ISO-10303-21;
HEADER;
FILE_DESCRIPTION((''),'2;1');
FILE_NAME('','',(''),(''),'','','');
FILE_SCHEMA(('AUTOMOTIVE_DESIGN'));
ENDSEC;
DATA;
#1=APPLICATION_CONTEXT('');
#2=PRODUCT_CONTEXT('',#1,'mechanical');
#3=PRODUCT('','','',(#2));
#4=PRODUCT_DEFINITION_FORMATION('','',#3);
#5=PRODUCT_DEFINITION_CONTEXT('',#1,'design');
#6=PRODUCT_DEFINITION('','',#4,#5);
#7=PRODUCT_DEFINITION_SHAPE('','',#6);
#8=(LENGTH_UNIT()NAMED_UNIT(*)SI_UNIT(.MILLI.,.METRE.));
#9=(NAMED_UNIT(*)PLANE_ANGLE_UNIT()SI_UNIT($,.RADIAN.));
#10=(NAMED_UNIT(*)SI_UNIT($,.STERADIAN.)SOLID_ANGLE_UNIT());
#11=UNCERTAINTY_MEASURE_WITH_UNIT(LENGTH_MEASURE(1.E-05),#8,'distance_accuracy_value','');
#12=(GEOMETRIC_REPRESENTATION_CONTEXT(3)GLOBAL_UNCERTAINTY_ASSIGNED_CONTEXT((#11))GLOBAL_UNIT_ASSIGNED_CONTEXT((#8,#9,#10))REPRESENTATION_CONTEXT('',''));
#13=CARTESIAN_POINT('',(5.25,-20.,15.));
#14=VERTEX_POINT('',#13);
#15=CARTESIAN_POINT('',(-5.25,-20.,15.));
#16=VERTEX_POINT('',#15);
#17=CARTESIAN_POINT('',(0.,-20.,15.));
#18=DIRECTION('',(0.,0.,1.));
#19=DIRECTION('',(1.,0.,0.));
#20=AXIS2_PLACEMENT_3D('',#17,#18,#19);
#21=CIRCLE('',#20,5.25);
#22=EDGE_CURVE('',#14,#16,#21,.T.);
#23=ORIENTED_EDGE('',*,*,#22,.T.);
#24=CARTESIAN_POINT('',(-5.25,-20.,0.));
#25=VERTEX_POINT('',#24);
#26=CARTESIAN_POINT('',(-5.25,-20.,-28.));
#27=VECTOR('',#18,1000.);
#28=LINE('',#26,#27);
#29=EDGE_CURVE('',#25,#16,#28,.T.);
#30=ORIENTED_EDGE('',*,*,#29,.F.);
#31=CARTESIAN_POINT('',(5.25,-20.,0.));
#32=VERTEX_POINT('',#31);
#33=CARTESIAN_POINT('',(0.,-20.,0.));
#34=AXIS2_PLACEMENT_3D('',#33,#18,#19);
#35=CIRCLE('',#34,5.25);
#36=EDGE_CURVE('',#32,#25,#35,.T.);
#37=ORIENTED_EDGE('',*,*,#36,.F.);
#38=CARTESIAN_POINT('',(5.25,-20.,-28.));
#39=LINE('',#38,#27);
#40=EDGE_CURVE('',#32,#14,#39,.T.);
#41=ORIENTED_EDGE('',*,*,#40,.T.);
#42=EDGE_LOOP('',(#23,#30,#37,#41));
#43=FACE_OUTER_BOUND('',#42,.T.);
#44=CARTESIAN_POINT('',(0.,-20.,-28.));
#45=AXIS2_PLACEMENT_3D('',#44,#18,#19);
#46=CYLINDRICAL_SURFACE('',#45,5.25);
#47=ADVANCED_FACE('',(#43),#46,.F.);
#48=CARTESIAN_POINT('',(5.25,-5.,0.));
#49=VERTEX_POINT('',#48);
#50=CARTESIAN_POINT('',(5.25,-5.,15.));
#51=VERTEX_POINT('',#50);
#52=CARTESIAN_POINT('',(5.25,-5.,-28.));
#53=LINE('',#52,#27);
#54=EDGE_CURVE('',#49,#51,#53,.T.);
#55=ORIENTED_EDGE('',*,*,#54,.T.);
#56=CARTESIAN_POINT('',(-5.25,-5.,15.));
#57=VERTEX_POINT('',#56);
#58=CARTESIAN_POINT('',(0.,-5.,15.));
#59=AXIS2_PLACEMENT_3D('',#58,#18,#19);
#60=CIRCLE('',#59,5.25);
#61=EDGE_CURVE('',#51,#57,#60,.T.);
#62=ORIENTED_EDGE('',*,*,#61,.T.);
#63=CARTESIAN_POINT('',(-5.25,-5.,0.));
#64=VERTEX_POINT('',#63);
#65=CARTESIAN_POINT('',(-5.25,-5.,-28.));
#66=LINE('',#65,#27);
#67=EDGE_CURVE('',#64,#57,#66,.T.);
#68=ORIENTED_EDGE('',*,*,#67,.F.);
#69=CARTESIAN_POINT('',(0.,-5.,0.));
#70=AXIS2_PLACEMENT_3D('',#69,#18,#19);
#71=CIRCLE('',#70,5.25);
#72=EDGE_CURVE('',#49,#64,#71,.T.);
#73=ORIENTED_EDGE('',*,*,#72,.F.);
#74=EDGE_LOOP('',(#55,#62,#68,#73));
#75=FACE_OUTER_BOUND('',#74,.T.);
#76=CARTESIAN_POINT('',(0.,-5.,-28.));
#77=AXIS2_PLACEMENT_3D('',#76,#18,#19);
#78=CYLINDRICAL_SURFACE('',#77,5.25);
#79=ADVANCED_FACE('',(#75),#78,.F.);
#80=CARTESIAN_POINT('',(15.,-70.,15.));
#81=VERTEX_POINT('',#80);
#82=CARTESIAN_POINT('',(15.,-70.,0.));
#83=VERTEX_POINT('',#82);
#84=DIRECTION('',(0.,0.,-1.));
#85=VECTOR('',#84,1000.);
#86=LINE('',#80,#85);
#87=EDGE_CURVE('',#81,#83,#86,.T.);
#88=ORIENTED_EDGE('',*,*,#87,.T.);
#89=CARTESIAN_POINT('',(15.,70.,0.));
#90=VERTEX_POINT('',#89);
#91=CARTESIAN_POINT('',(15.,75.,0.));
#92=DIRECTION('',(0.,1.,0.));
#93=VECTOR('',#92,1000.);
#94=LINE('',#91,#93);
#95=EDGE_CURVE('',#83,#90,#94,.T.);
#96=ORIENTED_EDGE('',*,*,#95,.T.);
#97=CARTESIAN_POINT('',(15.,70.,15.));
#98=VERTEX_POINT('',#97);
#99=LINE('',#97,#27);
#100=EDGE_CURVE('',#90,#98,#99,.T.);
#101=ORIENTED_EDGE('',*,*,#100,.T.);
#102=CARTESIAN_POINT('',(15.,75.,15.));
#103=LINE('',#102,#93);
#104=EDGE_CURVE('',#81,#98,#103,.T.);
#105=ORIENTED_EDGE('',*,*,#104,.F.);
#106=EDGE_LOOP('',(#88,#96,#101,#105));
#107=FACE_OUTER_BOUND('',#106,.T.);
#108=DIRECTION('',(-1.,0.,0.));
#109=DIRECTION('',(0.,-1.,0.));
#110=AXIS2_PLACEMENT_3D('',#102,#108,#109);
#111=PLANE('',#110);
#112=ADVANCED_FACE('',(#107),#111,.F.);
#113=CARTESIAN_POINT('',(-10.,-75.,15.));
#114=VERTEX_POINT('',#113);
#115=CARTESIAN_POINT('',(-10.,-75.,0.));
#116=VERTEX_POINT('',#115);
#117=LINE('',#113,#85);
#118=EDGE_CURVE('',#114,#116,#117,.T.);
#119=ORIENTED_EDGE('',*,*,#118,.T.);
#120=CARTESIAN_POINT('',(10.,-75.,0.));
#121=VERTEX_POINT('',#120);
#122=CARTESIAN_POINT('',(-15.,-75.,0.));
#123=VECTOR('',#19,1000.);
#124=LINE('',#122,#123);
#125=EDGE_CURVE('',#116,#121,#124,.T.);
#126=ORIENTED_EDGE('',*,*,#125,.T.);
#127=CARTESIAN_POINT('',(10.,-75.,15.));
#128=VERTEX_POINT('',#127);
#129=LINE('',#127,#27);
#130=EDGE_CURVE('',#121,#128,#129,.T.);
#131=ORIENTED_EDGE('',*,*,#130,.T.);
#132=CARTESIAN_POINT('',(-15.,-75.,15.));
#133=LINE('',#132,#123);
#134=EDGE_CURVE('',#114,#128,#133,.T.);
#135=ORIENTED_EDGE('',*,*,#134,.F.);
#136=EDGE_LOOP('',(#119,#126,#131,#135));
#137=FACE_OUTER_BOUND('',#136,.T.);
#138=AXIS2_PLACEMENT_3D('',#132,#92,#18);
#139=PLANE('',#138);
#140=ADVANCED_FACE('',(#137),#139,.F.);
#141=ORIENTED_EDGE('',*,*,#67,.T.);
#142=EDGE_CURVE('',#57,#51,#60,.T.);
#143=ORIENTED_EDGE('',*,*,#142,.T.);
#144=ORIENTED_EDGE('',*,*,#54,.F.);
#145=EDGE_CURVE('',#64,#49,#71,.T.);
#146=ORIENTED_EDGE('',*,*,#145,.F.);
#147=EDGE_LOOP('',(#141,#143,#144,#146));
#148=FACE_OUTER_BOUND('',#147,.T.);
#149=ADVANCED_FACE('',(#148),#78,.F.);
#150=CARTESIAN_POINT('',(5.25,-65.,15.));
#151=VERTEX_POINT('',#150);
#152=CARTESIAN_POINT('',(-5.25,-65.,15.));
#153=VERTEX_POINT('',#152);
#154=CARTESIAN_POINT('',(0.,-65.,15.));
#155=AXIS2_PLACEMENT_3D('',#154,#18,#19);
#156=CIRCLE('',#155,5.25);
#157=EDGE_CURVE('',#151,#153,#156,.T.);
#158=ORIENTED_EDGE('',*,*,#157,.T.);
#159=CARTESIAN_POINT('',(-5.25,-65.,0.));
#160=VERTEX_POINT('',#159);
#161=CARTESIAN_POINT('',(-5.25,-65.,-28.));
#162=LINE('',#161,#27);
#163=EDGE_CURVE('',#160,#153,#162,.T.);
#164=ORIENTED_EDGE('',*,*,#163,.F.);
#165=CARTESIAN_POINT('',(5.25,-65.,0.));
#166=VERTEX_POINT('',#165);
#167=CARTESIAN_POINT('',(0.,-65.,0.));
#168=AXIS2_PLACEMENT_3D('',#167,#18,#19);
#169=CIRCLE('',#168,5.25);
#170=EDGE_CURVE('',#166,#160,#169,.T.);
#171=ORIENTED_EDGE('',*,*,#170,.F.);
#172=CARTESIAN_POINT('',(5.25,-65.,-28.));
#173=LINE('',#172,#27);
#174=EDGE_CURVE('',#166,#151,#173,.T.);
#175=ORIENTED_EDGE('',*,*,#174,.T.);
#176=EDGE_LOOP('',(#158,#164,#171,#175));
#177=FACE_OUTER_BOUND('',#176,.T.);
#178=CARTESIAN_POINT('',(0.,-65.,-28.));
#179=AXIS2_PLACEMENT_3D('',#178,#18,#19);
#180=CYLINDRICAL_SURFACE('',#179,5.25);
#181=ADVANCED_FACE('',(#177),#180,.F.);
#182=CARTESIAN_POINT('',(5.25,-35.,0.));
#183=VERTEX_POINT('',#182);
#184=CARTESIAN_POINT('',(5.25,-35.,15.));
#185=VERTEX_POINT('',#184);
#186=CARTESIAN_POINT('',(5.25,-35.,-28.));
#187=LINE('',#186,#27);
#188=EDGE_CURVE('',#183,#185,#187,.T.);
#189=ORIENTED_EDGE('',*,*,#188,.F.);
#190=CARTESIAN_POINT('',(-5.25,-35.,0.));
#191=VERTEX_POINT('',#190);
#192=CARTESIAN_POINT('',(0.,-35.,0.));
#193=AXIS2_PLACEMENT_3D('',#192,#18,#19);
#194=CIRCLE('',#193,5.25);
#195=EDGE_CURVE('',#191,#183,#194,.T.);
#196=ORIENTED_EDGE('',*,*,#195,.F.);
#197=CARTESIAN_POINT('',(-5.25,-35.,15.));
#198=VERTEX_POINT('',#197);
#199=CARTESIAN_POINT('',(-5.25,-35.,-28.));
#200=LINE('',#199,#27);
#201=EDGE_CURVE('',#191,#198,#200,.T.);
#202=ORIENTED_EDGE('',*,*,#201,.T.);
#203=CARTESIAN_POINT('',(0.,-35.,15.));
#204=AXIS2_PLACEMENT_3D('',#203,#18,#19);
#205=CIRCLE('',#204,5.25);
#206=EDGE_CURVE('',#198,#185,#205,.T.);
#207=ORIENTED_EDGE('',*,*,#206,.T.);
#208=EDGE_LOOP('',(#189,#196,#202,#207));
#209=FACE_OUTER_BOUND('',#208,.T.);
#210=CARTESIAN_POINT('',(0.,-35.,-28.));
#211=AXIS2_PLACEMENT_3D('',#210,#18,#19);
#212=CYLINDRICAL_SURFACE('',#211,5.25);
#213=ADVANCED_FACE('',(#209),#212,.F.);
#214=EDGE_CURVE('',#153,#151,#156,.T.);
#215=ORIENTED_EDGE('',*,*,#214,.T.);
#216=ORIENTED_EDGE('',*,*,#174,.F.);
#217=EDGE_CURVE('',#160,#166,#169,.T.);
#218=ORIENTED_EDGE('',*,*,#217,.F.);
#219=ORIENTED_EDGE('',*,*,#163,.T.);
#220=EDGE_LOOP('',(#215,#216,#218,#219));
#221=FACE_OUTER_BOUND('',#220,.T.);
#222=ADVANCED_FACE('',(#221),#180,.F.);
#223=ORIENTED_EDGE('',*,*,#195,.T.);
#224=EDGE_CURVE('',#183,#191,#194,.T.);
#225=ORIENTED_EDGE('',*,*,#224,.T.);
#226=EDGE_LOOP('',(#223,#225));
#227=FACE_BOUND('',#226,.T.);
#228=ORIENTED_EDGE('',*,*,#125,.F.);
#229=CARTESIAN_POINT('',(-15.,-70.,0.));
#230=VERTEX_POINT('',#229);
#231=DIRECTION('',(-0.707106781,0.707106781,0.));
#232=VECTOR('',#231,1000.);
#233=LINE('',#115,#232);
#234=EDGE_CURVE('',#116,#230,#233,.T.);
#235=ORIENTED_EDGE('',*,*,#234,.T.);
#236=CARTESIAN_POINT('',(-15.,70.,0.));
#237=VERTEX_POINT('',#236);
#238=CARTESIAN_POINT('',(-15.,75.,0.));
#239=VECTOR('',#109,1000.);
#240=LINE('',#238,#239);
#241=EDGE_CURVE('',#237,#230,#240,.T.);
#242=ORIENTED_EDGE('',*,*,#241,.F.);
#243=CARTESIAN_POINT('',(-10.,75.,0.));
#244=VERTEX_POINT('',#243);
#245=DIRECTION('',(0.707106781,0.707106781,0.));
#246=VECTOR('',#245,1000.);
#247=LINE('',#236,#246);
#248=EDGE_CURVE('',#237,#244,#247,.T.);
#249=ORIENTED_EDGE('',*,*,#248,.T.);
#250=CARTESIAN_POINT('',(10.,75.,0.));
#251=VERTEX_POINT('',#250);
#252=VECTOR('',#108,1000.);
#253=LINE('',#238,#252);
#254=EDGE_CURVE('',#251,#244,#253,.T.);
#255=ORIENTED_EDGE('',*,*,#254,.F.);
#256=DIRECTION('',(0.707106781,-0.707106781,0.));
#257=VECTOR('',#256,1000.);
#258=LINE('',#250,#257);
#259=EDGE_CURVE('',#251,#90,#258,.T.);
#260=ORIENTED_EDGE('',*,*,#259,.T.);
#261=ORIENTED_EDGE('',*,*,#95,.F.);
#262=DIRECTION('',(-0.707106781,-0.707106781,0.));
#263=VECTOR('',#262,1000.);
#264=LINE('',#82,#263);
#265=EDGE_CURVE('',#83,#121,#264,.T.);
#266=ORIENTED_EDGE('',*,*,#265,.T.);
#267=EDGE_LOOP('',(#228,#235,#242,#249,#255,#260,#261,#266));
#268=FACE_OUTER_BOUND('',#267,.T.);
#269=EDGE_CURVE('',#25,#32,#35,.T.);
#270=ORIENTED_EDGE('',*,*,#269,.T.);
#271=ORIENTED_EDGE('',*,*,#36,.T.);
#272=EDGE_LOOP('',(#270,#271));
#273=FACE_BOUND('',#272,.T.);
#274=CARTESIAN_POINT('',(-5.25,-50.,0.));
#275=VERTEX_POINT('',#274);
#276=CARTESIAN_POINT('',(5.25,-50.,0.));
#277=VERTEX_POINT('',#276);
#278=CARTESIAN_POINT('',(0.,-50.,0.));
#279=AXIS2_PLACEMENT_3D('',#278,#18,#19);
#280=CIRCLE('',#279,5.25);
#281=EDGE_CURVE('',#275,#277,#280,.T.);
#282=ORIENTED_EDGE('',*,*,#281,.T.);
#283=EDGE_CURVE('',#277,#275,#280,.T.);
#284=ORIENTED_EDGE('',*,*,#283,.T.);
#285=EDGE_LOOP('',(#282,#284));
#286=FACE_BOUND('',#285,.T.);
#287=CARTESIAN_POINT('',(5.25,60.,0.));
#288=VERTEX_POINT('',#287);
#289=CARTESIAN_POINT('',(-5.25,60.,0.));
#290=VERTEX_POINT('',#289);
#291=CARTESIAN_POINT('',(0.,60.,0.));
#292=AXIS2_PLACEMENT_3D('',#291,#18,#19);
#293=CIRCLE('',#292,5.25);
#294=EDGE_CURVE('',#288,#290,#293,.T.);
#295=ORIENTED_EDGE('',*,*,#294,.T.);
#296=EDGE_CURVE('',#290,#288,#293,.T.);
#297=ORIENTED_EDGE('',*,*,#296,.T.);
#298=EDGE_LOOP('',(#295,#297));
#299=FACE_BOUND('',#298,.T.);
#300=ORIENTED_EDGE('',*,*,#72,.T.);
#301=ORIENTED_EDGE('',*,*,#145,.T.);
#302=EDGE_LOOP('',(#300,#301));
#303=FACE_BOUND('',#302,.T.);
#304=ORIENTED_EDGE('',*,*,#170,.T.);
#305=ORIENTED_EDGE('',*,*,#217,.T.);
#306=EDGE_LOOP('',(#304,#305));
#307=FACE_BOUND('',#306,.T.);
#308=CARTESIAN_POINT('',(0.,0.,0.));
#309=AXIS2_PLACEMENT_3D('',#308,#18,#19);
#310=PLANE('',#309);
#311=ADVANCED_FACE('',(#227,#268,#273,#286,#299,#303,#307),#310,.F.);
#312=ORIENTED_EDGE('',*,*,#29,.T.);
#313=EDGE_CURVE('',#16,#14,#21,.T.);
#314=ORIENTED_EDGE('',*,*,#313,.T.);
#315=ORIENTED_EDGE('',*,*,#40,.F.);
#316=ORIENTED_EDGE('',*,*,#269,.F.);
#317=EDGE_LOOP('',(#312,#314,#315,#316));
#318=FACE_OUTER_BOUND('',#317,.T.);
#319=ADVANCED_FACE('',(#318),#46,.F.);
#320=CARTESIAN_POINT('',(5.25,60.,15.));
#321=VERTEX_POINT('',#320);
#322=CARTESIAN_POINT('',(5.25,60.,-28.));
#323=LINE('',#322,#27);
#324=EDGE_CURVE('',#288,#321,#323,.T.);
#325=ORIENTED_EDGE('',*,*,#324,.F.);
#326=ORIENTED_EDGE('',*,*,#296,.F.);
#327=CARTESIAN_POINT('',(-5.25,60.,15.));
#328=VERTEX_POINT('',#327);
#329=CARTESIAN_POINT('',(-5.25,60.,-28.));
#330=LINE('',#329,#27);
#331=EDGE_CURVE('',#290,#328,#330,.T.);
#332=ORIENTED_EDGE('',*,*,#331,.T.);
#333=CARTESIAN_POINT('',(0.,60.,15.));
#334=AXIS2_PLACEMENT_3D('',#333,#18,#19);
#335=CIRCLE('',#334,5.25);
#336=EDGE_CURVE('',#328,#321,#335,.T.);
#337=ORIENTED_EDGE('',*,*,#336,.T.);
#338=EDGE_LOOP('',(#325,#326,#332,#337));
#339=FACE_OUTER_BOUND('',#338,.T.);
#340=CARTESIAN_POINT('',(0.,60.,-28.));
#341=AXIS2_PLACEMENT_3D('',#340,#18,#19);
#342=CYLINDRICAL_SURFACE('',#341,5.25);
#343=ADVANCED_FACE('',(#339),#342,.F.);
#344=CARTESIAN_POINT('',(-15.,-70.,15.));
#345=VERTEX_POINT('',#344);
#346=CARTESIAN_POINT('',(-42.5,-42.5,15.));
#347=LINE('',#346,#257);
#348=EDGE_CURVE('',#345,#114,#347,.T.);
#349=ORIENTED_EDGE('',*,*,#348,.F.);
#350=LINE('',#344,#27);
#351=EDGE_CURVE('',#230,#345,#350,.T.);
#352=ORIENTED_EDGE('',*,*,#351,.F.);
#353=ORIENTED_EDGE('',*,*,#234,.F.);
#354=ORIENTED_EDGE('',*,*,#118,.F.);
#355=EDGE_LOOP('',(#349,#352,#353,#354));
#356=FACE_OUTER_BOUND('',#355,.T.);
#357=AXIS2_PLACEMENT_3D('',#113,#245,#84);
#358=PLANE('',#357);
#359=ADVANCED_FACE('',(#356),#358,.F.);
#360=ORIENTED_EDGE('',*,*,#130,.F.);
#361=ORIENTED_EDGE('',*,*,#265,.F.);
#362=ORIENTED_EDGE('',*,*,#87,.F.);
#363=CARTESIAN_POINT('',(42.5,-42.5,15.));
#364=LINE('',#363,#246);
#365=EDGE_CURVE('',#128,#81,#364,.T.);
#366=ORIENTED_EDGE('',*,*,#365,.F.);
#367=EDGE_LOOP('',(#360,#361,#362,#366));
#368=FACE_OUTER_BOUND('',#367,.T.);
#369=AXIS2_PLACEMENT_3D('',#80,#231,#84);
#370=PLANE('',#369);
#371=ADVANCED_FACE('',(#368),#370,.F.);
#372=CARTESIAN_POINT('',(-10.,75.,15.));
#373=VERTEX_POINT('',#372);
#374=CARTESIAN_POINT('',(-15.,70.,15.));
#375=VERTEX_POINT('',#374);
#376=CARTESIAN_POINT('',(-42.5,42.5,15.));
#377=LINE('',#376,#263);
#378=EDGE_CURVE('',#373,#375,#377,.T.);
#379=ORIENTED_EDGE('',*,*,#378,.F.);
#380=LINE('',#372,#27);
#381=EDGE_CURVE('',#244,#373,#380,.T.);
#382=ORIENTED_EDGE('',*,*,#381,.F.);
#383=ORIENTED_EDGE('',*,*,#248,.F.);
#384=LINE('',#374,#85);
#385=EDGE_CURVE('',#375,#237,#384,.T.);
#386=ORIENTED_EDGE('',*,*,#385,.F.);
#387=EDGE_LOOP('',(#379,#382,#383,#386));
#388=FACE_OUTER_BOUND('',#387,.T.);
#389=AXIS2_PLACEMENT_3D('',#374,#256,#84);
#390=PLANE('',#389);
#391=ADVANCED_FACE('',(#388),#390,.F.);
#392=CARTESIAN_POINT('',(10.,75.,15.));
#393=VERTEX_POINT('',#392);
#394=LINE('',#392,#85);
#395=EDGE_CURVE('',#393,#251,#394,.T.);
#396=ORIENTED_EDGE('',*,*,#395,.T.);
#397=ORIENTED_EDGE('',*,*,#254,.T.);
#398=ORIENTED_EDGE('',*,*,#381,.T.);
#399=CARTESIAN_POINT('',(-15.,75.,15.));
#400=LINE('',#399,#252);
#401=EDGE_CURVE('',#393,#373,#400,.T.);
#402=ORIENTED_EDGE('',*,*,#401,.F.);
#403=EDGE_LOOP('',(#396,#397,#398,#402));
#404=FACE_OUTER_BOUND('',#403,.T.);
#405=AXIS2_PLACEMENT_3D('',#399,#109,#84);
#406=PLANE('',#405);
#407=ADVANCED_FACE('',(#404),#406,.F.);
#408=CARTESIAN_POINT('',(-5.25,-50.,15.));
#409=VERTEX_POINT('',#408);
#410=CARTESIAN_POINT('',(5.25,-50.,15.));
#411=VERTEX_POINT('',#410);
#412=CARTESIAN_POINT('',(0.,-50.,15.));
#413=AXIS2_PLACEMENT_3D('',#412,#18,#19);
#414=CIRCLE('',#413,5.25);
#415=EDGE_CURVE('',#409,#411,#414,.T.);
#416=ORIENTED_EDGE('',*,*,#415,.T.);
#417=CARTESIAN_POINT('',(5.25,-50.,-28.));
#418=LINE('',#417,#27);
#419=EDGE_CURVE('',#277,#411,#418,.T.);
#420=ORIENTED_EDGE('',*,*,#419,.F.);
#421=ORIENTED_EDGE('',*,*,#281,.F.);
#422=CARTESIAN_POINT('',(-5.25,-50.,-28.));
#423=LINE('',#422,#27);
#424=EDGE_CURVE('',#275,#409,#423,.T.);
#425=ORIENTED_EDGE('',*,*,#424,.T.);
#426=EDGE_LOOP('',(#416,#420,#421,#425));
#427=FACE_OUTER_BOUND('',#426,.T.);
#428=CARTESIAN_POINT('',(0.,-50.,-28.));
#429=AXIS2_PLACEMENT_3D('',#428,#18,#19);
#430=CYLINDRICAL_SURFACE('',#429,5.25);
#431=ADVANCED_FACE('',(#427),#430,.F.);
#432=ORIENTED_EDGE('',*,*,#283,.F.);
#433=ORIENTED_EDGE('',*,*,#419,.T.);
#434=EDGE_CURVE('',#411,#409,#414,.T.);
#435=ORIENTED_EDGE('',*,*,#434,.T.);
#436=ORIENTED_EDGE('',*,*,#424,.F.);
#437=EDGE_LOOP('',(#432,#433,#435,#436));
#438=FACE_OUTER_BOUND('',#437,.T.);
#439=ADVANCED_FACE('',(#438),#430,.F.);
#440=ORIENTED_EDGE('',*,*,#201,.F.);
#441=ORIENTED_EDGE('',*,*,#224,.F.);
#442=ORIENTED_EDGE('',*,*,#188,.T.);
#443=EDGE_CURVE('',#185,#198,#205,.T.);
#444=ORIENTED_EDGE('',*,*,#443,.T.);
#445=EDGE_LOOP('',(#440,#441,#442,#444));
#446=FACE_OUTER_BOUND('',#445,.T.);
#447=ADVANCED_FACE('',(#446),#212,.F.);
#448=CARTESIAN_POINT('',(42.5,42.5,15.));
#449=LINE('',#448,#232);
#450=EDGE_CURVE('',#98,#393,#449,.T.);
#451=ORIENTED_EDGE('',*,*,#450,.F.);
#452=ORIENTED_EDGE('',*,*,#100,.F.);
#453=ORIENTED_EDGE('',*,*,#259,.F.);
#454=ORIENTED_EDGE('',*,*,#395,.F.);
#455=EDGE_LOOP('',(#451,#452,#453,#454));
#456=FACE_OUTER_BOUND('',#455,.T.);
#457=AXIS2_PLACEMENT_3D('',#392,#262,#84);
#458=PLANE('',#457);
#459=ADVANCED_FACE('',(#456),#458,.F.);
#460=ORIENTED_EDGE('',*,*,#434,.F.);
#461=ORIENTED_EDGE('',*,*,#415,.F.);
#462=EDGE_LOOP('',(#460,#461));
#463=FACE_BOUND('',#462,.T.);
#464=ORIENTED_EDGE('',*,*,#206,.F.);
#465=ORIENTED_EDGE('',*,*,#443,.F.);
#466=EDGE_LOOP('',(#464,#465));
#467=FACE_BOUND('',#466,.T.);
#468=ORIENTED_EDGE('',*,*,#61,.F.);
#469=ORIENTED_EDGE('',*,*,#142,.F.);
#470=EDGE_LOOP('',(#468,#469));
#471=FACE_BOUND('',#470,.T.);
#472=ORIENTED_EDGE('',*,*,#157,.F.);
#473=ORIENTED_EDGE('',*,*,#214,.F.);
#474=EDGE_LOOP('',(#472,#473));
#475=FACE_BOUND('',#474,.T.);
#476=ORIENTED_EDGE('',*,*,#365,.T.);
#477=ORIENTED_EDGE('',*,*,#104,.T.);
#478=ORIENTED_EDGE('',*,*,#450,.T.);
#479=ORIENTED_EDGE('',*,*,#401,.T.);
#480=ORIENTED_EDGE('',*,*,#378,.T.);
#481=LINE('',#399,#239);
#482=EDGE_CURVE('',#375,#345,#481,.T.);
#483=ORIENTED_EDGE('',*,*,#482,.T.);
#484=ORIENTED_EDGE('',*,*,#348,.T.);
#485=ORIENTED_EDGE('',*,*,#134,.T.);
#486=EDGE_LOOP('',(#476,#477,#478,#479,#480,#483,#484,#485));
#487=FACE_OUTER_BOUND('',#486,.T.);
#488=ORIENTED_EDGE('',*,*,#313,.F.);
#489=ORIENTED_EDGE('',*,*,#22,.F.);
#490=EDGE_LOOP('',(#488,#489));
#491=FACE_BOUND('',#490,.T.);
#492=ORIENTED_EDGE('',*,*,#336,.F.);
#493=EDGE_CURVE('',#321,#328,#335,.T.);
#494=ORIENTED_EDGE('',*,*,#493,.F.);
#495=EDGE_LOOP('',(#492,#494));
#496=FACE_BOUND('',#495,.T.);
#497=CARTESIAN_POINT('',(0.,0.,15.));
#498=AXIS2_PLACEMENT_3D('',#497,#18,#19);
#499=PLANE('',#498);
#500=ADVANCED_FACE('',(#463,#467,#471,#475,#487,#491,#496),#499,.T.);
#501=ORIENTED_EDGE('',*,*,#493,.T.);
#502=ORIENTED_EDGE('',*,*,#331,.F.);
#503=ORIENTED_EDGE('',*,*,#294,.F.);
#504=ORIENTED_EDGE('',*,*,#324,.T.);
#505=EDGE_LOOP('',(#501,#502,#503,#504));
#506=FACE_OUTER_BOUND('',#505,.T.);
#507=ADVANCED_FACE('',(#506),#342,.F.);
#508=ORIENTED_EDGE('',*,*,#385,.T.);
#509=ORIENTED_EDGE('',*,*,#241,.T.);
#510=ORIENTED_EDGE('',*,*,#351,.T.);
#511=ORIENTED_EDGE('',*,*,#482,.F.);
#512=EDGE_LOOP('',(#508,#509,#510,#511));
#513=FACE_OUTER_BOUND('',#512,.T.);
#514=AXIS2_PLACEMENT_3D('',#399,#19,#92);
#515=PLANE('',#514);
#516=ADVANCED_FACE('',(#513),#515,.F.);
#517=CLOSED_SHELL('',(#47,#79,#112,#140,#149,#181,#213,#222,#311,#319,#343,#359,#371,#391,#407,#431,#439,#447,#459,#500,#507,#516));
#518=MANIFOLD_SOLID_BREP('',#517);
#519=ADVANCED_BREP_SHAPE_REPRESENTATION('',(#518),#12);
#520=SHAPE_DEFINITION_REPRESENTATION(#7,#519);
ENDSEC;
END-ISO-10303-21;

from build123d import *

# Parameters (mm, degrees)
SKETCH1_W           = 30
SKETCH1_H           = 150
BOSS_EXTRUDE1_DEPTH = 15
CHAMFER1_SIZE       = 5
SKETCH2_R           = 5.25
CUT_EXTRUDE1_DEPTH  = 43


with BuildPart() as part:
    # Sketch1 → Boss-Extrude1 (new body)
    with BuildSketch(Plane.XY):
        Rectangle(SKETCH1_W, SKETCH1_H)
    extrude(amount=BOSS_EXTRUDE1_DEPTH)

    # Chamfer1
    chamfer1_edges = [part.edges().sort_by_distance(p)[0] for p in [
        (15, -75, 7.5),
        (-15, -75, 7.5),
        (-15, 75, 7.5),
        (15, 75, 7.5),
    ]]
    chamfer(chamfer1_edges, length=CHAMFER1_SIZE)

    # Sketch2 → Cut-Extrude1 (cut)
    with BuildSketch(Plane.XY.offset(15)):
        with Locations((0, 60)):
            Circle(SKETCH2_R)
        with Locations((0, -5)):
            Circle(SKETCH2_R)
        with Locations((0, -20)):
            Circle(SKETCH2_R)
        with Locations((0, -35)):
            Circle(SKETCH2_R)
        with Locations((0, -50)):
            Circle(SKETCH2_R)
        with Locations((0, -65)):
            Circle(SKETCH2_R)
    extrude(amount=-CUT_EXTRUDE1_DEPTH, mode=Mode.SUBTRACT)


solid = part.part
